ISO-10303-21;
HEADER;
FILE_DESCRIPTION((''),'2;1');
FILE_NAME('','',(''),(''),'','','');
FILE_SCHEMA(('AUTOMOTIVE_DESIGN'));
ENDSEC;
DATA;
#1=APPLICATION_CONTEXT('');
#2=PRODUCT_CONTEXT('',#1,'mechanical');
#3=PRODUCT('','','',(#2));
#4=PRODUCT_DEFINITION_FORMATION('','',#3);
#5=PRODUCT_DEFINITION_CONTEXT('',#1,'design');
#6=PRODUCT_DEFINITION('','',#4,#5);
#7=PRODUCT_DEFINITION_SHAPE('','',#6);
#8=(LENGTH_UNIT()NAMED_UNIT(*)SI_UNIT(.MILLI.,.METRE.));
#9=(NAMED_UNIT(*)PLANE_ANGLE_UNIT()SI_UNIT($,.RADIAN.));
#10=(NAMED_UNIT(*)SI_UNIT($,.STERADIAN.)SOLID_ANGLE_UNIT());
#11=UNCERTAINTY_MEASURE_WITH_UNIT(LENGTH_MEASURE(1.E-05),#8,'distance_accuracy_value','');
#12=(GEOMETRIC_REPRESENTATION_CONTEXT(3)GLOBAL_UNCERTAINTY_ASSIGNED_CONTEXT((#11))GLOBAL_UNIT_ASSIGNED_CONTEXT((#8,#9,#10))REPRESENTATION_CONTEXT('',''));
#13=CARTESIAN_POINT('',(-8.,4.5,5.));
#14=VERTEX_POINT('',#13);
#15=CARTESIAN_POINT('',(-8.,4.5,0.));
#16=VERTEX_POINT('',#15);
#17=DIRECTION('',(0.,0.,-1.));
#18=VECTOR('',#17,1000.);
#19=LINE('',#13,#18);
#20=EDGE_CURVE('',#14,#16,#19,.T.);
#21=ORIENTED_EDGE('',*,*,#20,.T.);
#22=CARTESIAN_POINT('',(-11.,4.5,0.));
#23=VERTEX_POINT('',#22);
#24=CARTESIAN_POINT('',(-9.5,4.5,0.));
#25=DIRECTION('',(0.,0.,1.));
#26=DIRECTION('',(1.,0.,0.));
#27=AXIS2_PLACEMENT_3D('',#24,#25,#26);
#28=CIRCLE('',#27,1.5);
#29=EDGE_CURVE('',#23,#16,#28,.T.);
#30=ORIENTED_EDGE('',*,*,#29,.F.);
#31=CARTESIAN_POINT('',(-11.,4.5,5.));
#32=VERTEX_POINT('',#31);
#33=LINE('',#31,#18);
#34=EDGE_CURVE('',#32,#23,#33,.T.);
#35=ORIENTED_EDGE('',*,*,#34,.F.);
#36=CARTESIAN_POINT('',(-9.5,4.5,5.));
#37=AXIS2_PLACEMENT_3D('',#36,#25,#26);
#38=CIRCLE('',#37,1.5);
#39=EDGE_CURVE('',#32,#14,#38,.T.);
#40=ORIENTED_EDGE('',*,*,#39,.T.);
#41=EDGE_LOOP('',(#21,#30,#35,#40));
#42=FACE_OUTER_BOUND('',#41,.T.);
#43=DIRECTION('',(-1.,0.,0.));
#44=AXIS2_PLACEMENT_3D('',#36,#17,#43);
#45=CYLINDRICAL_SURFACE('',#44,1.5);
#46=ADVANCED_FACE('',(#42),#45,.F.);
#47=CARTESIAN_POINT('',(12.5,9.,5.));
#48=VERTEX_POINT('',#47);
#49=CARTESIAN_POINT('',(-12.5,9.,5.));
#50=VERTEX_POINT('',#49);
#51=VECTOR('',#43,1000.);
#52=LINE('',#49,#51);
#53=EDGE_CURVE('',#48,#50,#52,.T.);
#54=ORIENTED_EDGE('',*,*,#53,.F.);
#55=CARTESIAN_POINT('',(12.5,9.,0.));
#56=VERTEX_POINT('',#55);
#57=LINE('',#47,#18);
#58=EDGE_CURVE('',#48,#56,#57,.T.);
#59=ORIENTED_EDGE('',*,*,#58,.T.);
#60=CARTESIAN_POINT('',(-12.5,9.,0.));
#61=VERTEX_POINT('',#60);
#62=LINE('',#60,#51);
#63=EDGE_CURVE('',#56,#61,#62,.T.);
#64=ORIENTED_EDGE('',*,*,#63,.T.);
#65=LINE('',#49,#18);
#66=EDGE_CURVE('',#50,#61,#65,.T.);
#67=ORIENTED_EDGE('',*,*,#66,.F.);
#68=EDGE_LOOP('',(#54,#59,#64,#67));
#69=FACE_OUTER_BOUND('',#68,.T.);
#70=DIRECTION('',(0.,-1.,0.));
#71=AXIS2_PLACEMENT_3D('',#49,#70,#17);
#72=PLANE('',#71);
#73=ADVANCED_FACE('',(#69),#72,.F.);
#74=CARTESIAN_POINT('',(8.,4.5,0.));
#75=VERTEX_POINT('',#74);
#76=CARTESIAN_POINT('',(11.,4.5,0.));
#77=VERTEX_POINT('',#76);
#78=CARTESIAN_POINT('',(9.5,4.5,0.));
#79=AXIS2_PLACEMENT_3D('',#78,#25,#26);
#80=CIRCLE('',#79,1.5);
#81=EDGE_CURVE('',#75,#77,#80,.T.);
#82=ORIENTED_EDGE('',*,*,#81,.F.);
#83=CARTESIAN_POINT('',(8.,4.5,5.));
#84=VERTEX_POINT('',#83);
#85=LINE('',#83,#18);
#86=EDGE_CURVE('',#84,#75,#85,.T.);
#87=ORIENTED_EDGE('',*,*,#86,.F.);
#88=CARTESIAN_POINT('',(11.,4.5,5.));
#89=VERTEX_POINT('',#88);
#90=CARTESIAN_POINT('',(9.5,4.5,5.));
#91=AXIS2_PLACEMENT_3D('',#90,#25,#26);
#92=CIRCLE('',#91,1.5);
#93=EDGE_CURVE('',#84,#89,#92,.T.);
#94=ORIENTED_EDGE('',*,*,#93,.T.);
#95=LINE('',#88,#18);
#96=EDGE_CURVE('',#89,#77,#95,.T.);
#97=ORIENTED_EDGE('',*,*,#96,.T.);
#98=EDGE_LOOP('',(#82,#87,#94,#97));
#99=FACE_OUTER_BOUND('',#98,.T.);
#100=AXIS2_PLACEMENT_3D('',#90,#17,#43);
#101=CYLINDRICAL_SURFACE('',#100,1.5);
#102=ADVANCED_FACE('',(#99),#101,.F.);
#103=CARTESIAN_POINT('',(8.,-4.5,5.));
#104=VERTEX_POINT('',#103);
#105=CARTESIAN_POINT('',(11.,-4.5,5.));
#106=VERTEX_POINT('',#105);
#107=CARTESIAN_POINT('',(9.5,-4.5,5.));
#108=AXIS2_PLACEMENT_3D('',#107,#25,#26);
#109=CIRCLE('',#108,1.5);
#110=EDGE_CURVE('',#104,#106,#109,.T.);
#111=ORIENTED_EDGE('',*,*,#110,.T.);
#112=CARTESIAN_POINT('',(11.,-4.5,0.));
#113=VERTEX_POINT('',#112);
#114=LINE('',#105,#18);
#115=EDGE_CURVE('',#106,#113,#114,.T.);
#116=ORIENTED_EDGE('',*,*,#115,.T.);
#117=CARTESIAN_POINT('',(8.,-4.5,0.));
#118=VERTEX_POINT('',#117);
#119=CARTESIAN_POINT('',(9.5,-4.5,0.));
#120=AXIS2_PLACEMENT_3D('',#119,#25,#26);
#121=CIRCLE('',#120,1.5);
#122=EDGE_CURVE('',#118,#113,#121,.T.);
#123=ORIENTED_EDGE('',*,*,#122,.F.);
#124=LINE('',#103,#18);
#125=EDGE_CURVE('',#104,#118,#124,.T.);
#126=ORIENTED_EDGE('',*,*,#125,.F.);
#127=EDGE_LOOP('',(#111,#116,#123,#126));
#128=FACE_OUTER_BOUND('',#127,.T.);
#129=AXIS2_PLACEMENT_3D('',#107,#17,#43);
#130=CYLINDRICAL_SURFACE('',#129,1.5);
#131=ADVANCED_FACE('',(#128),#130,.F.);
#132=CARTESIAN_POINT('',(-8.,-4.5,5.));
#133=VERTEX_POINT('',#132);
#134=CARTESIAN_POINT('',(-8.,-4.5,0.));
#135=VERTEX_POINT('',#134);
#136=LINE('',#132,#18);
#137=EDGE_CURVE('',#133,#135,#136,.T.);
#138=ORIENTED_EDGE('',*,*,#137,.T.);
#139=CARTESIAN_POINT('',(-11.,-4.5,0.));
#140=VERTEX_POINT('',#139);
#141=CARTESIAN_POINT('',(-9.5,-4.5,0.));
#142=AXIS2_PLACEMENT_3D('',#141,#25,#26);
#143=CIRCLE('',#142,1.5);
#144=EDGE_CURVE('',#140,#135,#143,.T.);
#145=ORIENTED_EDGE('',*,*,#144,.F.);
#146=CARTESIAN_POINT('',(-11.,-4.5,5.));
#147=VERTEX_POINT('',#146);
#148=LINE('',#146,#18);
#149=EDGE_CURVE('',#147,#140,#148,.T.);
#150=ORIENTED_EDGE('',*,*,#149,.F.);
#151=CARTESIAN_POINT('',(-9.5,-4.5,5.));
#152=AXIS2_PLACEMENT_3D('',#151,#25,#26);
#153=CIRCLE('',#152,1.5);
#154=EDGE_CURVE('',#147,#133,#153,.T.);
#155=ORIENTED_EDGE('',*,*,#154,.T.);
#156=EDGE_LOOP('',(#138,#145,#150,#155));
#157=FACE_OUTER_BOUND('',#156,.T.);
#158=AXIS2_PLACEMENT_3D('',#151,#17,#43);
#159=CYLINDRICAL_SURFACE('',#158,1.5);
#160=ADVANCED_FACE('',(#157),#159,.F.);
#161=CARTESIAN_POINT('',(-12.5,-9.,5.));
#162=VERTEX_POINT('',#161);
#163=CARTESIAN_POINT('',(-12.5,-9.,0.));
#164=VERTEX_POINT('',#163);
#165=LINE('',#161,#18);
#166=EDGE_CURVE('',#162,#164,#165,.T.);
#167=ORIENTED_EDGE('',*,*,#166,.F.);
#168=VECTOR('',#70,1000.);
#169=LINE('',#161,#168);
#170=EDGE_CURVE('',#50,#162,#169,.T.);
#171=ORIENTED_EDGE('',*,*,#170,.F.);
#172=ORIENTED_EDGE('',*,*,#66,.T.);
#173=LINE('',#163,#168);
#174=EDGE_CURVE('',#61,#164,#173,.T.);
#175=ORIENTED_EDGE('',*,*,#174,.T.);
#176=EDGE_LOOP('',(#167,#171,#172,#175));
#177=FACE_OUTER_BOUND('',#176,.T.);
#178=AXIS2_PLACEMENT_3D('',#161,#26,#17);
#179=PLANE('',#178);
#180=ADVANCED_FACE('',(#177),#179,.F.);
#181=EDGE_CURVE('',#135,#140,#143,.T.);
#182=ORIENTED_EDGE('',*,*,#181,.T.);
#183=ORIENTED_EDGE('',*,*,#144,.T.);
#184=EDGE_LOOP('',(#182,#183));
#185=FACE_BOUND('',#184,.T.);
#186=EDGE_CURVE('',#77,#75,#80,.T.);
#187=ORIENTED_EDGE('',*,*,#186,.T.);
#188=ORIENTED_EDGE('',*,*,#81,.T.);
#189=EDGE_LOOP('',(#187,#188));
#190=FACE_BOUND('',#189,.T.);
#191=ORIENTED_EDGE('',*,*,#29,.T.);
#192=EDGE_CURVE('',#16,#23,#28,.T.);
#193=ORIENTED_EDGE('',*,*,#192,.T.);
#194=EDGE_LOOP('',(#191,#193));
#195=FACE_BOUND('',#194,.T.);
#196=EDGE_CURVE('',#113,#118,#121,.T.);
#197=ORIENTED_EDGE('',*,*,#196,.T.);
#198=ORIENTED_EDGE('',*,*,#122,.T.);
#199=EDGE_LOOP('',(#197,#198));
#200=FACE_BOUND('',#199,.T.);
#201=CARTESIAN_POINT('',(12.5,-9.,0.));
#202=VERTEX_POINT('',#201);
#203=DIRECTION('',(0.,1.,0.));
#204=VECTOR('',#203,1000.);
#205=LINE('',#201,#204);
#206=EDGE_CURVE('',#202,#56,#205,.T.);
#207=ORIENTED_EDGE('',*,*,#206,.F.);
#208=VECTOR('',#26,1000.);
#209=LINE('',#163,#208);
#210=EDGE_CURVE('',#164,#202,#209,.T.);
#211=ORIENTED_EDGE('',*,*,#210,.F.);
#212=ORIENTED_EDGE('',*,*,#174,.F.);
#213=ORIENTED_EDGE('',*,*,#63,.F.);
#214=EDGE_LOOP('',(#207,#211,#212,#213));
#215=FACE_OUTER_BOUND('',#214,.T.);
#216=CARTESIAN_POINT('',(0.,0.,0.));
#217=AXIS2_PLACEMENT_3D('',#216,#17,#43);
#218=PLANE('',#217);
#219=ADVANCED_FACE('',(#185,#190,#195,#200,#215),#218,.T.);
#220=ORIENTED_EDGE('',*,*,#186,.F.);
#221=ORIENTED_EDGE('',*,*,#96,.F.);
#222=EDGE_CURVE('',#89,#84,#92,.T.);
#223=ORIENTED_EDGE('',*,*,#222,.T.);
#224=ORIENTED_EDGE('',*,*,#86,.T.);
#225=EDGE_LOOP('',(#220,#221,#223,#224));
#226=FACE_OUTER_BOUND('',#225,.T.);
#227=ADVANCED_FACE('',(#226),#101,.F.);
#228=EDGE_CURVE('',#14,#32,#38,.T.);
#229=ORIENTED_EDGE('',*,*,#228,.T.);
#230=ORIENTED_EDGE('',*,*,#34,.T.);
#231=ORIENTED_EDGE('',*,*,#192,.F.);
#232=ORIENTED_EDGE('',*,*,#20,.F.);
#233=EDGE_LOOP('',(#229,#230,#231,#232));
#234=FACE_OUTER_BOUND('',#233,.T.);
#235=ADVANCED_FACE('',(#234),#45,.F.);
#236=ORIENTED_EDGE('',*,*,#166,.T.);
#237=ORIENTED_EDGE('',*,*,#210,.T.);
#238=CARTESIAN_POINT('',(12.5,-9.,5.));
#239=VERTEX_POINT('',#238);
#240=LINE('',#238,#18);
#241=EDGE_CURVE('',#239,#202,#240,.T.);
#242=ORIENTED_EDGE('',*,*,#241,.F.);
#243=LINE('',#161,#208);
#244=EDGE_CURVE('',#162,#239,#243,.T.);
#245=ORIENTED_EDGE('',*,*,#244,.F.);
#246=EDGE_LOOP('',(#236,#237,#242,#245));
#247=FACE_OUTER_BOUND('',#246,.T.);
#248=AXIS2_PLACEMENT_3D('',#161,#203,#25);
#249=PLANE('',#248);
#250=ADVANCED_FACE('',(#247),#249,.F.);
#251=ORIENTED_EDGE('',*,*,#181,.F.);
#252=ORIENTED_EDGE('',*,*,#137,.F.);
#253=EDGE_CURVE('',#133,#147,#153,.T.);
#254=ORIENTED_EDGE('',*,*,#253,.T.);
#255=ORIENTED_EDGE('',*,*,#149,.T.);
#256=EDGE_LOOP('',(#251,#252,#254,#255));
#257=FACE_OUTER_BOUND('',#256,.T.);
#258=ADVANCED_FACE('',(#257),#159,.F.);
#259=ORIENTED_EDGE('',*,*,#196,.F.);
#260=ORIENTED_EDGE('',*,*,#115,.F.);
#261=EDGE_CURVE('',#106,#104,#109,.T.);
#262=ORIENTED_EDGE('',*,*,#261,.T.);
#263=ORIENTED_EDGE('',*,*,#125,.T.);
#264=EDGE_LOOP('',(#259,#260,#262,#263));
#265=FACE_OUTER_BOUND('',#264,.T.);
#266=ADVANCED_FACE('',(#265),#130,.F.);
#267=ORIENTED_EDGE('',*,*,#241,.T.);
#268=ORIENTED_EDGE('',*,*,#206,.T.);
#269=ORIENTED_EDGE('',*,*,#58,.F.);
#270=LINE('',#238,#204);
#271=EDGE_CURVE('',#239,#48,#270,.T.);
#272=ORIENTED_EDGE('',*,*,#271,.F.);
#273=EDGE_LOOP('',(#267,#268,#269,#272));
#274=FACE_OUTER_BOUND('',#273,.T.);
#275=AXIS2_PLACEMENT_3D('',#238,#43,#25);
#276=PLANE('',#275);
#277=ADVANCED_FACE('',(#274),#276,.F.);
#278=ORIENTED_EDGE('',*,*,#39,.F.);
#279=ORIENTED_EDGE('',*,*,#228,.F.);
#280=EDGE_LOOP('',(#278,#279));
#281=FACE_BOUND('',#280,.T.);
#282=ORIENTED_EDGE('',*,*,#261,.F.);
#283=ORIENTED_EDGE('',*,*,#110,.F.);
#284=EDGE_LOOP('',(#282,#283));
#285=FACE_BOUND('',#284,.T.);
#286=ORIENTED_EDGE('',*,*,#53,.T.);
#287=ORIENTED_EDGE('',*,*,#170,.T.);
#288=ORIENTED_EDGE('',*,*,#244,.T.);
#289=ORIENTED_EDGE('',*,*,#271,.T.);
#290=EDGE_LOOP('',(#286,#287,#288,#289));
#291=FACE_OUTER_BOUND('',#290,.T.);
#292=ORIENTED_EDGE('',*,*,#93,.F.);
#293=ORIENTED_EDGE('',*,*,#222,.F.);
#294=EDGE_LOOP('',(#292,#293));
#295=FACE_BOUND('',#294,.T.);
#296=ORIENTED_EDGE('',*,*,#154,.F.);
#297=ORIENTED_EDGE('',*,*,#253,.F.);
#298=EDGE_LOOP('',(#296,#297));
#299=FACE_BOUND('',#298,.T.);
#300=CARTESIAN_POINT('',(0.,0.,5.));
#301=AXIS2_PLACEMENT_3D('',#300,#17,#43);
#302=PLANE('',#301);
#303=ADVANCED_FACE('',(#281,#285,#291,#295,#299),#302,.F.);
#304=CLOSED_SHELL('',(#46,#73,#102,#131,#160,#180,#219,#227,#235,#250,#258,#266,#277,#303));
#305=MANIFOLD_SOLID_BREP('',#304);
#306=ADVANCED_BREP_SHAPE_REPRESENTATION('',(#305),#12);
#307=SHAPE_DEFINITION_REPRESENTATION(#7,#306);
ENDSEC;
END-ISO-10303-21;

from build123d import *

# Parameters (mm, degrees)
SKETCH1_W           = 25
SKETCH1_H           = 18
SKETCH1_R           = 1.5
BOSS_EXTRUDE1_DEPTH = 5


with BuildPart() as part:
    # Sketch1 → Boss-Extrude1 (new body)
    with BuildSketch(Plane.XY):
        Rectangle(SKETCH1_W, SKETCH1_H)
        with Locations((-9.5, 4.5)):
            Circle(SKETCH1_R, mode=Mode.SUBTRACT)
        with Locations((9.5, 4.5)):
            Circle(SKETCH1_R, mode=Mode.SUBTRACT)
        with Locations((9.5, -4.5)):
            Circle(SKETCH1_R, mode=Mode.SUBTRACT)
        with Locations((-9.5, -4.5)):
            Circle(SKETCH1_R, mode=Mode.SUBTRACT)
    extrude(amount=BOSS_EXTRUDE1_DEPTH)


solid = part.part
